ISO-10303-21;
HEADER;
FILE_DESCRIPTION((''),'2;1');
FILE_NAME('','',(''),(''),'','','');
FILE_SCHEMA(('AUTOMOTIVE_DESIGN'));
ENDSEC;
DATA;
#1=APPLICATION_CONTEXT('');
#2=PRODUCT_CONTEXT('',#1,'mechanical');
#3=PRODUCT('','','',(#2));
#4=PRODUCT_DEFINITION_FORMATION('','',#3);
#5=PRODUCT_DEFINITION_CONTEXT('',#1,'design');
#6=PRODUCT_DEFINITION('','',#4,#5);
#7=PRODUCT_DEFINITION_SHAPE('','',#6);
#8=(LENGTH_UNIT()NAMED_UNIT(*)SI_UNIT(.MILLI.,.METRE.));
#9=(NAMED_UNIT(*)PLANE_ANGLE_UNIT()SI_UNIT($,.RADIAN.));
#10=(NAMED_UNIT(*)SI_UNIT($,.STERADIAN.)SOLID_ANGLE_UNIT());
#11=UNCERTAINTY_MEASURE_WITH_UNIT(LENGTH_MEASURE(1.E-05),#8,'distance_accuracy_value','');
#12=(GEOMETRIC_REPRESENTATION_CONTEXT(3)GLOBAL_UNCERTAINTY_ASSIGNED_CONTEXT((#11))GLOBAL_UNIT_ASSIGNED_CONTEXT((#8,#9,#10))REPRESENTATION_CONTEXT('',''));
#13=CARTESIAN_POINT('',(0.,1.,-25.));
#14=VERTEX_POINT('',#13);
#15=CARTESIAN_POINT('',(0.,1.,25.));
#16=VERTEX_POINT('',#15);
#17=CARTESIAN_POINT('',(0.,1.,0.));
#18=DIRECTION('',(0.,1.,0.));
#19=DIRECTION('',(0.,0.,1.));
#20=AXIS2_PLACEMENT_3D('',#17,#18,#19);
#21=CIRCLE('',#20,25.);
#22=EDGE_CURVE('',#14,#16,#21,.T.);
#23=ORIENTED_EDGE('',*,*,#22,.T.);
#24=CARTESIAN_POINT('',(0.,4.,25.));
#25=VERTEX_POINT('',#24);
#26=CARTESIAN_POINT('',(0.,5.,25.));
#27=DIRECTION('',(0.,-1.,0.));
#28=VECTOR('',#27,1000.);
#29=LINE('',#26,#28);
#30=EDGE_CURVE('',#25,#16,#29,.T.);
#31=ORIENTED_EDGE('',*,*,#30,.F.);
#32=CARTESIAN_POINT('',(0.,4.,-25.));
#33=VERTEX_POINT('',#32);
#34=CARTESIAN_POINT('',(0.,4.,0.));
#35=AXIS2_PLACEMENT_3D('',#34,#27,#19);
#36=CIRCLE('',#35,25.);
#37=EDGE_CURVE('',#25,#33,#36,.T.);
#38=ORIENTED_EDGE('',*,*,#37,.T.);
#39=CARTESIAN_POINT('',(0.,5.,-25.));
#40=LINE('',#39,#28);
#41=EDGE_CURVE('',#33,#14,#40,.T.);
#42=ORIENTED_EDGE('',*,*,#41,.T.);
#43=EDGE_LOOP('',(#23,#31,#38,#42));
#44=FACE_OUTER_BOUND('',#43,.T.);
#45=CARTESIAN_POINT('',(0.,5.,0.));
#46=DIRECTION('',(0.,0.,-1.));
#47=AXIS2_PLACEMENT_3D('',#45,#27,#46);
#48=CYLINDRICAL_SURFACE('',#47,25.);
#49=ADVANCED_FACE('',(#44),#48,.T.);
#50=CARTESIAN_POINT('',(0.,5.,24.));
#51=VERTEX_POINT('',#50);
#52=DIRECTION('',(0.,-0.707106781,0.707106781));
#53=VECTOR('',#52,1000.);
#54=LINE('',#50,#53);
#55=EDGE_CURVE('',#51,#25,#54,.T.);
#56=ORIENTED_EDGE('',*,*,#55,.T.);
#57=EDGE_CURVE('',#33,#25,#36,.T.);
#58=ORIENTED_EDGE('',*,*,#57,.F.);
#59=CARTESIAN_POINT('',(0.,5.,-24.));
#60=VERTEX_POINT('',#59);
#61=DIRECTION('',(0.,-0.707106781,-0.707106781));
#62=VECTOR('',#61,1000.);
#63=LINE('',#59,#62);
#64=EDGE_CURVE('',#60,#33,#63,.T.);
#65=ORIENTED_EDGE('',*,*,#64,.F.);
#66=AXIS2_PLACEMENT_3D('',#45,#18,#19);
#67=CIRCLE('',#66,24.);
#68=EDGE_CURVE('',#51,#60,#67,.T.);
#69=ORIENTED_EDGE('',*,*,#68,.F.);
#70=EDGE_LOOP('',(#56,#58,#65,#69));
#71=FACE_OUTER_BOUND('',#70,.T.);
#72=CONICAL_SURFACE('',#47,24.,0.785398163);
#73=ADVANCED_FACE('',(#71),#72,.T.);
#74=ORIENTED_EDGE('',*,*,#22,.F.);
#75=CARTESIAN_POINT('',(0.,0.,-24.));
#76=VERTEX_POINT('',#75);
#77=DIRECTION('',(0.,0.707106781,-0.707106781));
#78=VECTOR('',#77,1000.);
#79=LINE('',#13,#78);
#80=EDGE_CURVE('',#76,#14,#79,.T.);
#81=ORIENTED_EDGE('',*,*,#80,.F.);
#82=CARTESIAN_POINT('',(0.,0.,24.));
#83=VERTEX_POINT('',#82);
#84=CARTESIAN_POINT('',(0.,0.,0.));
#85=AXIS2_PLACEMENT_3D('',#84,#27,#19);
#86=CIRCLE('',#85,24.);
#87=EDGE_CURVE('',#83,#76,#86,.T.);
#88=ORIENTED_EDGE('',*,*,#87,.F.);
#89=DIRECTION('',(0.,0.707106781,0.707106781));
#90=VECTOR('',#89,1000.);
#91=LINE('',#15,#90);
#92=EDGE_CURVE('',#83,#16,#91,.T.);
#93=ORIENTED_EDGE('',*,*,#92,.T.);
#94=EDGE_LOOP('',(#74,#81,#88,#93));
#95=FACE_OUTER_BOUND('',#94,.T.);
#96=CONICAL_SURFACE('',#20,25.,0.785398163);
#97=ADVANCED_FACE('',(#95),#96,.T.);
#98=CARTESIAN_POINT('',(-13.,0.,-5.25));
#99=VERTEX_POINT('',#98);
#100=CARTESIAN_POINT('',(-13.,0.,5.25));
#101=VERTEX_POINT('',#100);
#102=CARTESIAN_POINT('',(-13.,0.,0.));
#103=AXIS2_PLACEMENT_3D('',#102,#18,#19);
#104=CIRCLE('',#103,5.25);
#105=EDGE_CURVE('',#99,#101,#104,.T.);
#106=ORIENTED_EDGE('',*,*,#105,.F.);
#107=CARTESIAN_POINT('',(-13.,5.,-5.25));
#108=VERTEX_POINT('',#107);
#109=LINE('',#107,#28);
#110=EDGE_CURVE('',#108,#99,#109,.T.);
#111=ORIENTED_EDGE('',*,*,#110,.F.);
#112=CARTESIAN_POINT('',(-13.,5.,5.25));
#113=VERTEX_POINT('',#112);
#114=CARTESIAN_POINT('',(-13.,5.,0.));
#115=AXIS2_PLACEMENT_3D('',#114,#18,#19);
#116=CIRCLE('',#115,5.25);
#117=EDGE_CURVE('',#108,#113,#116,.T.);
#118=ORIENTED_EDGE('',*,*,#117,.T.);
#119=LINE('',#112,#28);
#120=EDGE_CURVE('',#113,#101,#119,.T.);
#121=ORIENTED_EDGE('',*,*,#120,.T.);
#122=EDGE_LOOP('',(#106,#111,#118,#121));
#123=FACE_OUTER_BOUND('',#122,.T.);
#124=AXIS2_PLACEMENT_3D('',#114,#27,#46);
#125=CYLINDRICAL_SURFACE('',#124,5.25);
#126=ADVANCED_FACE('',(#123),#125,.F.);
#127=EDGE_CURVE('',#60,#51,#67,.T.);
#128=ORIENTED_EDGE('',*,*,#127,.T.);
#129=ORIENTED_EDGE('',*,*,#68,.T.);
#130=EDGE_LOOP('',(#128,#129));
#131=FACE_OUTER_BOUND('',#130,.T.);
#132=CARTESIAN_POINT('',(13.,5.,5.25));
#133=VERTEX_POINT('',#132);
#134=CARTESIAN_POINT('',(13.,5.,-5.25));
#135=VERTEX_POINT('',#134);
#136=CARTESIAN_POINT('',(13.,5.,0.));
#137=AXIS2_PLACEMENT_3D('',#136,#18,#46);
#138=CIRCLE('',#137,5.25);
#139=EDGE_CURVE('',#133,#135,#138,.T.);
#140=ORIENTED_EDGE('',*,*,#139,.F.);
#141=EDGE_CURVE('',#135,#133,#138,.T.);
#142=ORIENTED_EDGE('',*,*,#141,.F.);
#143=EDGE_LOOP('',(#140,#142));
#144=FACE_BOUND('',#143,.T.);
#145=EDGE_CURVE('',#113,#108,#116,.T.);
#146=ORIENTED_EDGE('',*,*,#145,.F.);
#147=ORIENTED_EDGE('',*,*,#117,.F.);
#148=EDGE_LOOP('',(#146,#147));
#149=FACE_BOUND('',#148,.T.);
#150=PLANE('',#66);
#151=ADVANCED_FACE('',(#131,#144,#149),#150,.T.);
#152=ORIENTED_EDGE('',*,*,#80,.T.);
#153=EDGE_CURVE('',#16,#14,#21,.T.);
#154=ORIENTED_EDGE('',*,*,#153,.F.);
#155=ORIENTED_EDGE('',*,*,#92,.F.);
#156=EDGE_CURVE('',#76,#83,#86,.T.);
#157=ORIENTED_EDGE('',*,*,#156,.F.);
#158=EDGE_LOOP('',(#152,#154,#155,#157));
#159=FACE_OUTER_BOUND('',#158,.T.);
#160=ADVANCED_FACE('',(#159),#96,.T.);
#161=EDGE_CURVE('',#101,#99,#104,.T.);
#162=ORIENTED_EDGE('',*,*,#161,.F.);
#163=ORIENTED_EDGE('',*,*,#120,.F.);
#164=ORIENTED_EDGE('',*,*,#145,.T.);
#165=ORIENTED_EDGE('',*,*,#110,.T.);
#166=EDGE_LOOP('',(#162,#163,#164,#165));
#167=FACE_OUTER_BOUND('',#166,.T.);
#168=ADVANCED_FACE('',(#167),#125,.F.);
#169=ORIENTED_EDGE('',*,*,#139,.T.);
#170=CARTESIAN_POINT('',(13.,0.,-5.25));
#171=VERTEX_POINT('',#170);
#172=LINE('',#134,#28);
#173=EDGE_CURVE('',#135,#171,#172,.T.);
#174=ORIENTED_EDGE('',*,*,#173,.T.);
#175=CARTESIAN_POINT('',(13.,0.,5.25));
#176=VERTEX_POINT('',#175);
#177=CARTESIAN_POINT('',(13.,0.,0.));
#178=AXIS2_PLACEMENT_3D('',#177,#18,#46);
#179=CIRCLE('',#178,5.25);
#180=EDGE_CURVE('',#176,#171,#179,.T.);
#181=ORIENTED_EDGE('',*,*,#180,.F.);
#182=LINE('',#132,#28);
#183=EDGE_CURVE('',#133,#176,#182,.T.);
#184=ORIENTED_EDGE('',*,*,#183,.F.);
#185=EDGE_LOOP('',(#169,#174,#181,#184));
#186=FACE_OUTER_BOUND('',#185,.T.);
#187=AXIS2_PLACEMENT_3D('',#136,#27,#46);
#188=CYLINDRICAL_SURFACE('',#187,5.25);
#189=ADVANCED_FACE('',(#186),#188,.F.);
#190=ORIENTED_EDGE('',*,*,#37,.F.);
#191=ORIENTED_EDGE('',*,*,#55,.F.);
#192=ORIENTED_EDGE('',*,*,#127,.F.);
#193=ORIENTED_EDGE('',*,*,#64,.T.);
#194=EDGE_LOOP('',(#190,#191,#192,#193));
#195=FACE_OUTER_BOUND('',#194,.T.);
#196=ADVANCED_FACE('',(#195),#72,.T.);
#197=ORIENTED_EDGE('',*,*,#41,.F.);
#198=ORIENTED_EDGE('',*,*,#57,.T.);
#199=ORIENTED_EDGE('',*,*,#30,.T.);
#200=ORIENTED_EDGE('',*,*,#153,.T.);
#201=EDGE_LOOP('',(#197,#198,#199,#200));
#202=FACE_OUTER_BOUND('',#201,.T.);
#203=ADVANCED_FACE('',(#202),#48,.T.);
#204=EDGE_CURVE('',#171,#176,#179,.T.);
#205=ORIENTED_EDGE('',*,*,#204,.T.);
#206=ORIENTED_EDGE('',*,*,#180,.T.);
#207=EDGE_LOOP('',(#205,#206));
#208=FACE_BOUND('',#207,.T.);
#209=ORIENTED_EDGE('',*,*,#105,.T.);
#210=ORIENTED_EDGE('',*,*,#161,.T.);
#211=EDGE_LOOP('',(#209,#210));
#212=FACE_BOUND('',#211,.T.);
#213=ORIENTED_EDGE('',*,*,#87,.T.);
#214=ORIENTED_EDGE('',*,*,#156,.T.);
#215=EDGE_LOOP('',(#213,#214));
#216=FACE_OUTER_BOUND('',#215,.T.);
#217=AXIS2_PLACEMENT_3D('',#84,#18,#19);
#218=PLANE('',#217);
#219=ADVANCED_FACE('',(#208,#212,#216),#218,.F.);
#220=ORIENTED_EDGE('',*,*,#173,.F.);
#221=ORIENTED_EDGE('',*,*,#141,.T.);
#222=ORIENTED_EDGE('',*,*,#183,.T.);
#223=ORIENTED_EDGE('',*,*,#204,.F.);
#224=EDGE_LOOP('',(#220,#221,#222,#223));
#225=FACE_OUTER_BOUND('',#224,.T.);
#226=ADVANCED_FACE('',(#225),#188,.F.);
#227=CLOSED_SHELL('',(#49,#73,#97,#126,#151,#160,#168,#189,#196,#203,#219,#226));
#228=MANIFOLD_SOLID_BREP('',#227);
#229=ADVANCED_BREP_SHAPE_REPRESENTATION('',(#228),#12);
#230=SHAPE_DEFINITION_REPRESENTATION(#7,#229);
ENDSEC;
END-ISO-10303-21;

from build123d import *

# Parameters (mm, degrees)
SKETCH1_R           = 25
SKETCH1_R_2         = 5.25
BOSS_EXTRUDE1_DEPTH = 5
CHAMFER1_SIZE       = 1


with BuildPart() as part:
    # Sketch1 → Boss-Extrude1 (new body)
    with BuildSketch(Plane(origin=(0, 0, 0), x_dir=(1, 0, 0), z_dir=(0, 1, 0))):
        with Locations(Location((0, 0, 0), (0, 0, 270))):
            Circle(SKETCH1_R)
        with Locations(Location((-13, 0, 0), (0, 0, 270))):
            Circle(SKETCH1_R_2, mode=Mode.SUBTRACT)
        with Locations(Location((13, 0, 0), (0, 0, 90))):
            Circle(SKETCH1_R_2, mode=Mode.SUBTRACT)
    extrude(amount=BOSS_EXTRUDE1_DEPTH)

    # Chamfer1
    chamfer1_edges = [part.edges().sort_by_distance(p)[0] for p in [
        (0, 0, -25),
        (0, 5, -25),
    ]]
    chamfer(chamfer1_edges, length=CHAMFER1_SIZE)


solid = part.part
